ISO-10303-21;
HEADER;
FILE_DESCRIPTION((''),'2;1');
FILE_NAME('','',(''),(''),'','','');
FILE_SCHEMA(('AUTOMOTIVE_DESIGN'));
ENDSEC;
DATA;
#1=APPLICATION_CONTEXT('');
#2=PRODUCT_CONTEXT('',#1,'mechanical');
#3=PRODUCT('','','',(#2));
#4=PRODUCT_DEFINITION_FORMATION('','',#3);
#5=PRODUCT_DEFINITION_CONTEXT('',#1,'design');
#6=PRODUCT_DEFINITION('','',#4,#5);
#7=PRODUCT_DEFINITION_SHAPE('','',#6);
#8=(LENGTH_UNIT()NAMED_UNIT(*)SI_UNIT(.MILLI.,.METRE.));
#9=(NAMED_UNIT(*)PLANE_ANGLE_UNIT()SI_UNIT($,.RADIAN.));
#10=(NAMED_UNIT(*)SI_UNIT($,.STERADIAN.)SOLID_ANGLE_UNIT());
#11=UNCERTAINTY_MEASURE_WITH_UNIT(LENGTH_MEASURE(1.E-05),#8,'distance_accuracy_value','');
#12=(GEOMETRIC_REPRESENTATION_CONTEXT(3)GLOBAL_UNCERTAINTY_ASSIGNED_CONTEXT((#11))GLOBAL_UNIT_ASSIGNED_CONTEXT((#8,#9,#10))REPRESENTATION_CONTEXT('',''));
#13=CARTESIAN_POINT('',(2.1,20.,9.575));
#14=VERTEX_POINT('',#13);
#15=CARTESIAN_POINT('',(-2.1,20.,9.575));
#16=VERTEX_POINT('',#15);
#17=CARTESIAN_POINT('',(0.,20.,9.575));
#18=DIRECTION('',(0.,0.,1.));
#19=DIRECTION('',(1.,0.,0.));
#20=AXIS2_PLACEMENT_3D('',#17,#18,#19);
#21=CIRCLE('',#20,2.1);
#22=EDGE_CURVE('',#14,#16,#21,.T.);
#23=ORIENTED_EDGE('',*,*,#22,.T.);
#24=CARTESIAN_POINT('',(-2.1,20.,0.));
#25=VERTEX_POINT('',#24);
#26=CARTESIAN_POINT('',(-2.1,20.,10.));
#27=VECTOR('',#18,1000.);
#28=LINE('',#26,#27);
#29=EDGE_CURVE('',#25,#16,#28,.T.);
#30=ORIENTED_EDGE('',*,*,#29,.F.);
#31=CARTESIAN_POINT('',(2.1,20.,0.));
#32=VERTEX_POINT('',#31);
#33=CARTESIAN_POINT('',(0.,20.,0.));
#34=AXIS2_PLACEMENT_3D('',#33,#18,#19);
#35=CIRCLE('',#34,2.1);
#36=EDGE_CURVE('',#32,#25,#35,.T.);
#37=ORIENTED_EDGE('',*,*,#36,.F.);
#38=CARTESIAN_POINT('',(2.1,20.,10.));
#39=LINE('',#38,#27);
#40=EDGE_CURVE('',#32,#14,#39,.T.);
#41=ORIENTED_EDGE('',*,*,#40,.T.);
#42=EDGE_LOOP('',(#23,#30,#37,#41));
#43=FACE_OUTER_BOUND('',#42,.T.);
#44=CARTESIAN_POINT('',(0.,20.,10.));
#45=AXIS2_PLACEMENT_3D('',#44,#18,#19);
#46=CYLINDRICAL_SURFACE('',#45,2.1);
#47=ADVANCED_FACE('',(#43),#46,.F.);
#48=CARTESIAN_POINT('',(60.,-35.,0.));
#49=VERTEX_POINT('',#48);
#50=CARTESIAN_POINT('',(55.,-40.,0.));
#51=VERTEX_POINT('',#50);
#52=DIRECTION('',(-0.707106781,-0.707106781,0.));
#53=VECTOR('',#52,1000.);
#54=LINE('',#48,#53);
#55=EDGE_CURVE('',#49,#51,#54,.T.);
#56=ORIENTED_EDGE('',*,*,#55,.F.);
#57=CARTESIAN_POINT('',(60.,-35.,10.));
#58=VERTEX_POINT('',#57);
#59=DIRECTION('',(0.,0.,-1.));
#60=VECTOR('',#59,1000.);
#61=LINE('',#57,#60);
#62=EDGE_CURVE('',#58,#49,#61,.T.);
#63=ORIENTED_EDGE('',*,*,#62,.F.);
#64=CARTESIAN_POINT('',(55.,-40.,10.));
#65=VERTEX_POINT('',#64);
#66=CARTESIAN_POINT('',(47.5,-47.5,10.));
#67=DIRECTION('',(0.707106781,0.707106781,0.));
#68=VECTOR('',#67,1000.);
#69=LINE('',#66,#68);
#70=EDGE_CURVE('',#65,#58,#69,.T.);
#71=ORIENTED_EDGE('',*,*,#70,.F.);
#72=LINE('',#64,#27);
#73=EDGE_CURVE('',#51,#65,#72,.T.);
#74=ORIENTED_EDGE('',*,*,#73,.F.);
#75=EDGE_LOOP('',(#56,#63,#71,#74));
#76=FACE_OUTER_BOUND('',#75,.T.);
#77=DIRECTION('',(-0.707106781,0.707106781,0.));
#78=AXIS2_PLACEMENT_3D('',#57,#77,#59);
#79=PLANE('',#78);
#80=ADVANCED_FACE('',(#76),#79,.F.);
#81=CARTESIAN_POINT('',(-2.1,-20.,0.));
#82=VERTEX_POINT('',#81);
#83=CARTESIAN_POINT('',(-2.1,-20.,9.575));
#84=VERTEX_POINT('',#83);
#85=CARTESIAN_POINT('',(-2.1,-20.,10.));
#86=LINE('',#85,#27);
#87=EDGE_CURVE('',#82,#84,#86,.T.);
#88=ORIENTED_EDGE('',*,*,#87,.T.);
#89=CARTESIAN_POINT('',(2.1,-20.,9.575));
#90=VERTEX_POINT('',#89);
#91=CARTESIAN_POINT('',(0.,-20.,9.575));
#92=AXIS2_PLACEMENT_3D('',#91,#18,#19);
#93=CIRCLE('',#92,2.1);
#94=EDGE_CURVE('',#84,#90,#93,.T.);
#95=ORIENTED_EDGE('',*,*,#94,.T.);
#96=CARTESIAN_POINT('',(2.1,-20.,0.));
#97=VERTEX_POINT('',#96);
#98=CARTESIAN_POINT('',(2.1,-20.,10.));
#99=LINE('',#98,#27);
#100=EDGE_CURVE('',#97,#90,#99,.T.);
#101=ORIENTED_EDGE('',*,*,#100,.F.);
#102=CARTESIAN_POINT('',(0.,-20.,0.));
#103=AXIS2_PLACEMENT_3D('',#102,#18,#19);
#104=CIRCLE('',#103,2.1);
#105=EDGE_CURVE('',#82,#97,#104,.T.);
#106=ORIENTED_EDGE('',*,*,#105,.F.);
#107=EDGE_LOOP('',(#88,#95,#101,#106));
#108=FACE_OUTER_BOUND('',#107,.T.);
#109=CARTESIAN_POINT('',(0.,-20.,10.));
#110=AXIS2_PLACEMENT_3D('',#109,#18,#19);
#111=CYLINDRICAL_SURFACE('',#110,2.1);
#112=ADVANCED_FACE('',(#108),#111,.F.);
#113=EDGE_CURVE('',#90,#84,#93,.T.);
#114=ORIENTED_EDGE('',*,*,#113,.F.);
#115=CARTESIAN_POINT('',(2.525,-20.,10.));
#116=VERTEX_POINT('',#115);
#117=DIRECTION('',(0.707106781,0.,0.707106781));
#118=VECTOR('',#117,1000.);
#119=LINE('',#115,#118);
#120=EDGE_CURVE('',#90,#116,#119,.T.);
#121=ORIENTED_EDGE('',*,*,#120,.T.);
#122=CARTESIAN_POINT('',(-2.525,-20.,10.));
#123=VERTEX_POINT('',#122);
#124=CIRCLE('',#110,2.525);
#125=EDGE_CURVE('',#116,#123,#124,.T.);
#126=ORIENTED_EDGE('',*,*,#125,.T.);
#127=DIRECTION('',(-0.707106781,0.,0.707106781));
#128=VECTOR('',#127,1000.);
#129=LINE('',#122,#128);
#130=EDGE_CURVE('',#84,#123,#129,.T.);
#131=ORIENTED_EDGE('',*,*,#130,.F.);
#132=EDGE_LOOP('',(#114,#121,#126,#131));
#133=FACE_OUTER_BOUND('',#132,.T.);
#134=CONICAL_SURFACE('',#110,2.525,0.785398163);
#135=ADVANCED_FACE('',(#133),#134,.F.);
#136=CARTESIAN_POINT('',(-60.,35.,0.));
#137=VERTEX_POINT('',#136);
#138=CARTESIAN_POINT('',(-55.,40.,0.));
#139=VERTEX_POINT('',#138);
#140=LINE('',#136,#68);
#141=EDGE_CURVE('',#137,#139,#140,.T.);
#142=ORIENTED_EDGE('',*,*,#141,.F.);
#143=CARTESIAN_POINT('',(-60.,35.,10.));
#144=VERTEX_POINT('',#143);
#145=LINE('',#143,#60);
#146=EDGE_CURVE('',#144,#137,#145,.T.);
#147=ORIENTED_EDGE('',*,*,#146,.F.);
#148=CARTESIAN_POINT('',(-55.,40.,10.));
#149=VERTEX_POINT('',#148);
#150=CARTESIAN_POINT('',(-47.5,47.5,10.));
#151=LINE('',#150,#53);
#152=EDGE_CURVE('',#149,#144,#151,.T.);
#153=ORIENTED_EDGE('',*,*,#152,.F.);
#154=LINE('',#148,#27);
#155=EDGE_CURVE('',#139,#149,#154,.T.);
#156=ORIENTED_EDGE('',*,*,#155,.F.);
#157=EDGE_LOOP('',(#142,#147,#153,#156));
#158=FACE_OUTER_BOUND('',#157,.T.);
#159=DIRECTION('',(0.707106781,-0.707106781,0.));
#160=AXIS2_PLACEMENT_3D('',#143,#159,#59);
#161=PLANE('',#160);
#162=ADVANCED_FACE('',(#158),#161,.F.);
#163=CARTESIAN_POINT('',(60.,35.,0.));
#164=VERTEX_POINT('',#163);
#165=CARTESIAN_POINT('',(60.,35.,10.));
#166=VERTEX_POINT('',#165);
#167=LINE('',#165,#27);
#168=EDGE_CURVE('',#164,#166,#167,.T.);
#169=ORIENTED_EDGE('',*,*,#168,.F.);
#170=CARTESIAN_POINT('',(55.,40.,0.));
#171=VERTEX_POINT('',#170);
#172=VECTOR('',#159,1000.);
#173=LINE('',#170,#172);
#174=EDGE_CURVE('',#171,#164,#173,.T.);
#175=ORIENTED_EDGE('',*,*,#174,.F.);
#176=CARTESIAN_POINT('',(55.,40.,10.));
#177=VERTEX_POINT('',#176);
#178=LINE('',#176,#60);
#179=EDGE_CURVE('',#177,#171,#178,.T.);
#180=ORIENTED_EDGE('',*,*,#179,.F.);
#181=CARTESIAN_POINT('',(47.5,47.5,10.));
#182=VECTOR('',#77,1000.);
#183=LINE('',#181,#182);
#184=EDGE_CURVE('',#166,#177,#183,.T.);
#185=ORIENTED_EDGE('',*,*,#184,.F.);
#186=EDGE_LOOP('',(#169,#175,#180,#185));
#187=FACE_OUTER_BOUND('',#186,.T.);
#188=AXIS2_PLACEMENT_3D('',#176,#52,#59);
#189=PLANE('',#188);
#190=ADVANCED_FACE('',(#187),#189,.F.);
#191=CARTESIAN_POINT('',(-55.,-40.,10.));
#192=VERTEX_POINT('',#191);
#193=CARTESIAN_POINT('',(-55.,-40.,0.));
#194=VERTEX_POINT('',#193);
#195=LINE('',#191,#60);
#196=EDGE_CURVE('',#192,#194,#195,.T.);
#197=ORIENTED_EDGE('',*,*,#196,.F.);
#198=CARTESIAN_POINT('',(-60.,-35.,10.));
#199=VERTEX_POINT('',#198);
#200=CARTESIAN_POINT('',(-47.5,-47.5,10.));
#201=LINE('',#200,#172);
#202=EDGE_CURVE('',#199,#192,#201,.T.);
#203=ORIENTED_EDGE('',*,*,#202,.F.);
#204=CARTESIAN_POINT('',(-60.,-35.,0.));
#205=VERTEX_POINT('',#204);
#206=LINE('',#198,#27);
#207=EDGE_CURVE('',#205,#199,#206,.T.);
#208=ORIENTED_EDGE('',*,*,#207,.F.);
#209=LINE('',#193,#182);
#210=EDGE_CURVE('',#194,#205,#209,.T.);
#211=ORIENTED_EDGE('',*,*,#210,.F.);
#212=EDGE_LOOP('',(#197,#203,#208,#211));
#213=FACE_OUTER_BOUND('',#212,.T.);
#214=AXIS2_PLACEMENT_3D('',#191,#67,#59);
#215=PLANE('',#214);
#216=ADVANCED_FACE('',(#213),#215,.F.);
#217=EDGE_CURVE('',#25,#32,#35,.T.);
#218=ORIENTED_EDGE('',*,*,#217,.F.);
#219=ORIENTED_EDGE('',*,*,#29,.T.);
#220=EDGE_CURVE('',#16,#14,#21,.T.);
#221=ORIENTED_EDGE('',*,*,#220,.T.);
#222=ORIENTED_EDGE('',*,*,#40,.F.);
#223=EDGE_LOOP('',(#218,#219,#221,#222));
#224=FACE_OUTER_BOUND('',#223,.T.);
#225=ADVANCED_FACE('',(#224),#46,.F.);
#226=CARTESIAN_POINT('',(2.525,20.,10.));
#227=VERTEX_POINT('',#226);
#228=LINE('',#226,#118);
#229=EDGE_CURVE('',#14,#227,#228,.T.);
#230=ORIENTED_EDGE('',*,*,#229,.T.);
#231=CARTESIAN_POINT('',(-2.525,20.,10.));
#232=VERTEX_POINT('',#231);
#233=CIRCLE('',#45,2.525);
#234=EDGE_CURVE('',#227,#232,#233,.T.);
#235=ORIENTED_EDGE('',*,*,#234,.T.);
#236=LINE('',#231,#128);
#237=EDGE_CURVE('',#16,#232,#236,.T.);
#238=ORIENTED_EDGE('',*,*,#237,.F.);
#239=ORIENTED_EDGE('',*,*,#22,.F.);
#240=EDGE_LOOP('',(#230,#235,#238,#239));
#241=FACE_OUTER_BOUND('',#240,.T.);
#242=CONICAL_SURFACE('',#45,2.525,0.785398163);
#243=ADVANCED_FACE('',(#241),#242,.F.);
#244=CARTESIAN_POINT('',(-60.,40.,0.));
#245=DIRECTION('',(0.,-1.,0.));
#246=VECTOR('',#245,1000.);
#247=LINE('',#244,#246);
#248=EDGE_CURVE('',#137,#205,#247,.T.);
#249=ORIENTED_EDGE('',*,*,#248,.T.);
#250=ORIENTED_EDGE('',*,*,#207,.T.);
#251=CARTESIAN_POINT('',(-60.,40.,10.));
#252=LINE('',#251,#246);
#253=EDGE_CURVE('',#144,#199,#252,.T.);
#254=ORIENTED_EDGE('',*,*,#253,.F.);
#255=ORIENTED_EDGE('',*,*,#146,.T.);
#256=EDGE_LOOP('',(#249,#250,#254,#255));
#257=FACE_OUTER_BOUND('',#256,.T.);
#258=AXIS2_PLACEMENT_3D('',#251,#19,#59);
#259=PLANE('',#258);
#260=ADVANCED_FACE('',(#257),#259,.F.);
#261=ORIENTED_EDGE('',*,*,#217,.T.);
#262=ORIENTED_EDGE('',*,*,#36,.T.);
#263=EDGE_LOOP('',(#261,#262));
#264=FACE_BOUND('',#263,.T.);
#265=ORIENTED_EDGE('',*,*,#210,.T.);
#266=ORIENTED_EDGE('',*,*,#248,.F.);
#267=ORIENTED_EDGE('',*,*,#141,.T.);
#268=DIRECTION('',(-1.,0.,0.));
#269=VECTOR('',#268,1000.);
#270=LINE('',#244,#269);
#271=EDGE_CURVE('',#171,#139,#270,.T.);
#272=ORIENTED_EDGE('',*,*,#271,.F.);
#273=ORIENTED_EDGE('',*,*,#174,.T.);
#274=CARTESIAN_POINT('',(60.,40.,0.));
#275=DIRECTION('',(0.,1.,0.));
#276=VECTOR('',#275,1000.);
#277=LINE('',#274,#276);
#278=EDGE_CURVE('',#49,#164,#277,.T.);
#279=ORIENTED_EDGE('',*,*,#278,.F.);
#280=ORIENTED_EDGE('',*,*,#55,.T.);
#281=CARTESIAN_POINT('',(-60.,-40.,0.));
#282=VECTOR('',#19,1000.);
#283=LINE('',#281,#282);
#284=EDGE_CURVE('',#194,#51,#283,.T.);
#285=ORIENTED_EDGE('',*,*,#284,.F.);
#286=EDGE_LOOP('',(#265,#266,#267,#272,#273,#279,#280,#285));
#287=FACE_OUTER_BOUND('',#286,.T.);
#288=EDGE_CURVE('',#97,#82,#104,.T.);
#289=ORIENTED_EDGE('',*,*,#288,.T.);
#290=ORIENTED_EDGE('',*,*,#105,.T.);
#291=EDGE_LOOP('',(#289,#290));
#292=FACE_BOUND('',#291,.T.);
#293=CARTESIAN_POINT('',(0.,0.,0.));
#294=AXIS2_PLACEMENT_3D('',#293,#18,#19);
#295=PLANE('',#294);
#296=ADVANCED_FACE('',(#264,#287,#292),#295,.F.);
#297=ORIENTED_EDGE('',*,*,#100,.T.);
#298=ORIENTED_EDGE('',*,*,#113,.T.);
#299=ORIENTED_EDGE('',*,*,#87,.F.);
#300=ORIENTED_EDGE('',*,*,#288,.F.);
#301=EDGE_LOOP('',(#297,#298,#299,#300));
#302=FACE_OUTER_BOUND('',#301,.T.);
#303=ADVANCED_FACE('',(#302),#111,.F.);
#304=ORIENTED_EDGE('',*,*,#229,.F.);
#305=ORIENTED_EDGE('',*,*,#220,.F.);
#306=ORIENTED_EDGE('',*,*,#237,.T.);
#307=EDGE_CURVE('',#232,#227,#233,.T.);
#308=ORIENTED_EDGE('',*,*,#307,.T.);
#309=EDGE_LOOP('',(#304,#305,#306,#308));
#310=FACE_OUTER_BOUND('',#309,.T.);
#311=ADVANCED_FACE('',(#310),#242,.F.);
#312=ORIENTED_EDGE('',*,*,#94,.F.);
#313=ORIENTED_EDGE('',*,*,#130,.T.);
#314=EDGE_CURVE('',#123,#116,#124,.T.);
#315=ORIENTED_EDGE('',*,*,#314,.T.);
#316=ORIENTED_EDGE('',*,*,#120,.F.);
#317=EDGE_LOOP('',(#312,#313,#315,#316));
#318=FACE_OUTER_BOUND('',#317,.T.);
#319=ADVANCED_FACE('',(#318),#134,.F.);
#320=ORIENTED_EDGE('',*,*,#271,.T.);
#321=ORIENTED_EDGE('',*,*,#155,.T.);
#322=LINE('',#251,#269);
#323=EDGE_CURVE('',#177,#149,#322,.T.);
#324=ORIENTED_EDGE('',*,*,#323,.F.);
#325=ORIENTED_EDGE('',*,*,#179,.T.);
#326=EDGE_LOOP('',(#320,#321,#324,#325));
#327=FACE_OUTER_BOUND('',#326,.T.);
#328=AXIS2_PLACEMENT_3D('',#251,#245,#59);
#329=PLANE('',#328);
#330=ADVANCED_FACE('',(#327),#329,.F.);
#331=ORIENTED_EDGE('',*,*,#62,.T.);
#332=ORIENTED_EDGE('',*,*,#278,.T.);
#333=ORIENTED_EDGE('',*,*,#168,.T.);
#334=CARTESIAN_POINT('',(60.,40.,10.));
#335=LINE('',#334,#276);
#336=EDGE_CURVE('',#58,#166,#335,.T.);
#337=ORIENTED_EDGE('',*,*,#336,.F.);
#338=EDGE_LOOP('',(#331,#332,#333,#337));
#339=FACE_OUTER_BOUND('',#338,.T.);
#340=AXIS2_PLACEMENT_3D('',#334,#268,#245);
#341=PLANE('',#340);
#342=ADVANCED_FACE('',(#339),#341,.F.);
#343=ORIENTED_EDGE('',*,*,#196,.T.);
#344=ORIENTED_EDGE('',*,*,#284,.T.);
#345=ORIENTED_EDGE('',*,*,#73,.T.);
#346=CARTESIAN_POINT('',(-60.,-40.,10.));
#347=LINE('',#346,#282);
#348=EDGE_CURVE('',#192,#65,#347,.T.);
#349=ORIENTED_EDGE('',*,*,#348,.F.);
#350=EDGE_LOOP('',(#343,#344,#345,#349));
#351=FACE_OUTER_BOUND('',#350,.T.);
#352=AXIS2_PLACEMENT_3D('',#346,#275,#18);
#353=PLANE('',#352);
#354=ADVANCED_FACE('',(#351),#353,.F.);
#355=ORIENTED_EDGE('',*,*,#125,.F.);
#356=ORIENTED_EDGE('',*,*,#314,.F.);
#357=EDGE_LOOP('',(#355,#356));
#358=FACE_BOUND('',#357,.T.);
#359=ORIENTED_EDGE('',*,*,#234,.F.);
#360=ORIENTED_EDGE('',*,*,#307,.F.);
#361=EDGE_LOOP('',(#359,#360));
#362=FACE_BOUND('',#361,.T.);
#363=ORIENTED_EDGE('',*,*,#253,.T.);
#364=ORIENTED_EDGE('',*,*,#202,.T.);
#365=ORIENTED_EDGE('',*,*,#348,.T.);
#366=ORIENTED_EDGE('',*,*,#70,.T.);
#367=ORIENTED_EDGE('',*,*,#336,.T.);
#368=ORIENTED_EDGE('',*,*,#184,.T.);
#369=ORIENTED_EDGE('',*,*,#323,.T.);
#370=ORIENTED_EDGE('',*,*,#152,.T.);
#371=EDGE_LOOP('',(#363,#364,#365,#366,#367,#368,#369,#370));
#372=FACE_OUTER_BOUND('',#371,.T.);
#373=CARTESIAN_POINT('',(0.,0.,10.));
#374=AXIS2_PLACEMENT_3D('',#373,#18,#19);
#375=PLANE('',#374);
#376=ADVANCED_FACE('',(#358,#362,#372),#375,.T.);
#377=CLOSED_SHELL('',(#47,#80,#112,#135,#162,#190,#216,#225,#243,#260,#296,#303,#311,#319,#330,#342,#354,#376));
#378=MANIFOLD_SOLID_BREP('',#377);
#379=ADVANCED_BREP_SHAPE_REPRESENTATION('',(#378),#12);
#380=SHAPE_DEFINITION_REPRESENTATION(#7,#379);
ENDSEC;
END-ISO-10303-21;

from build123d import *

# Parameters (mm, degrees)
SKETCH_1_W                   = 120
SKETCH_1_H                   = 80
EXTRUDE_1_DEPTH              = 10
CHAMFER_1_SIZE               = 5
HOLE_WIZARD_M5_1_D           = 4.2
HOLE_WIZARD_M5_1_DEPTH       = 14
HOLE_WIZARD_M5_1_CSINK_D     = 5.05
HOLE_WIZARD_M5_1_CSINK_ANGLE = 90
HOLE_WIZARD_M5_1_TIP         = 1.2618073


with BuildPart() as part:
    # 草图1 → 凸台-拉伸1 (new body)
    with BuildSketch(Plane.XY):
        Rectangle(SKETCH_1_W, SKETCH_1_H)
    extrude(amount=EXTRUDE_1_DEPTH)

    # 倒角1
    chamfer_1_edges = [part.edges().sort_by_distance(p)[0] for p in [
        (60, -40, 5),
        (-60, -40, 5),
        (-60, 40, 5),
        (60, 40, 5),
    ]]
    chamfer(chamfer_1_edges, length=CHAMFER_1_SIZE)

    # M5 螺纹孔1
    with Locations(Plane(origin=(0, 20, 10), x_dir=(1, 0, 0), z_dir=(0, 0, 1))):
        with Locations((0, 0), (0, -40)):
            CounterSinkHole(HOLE_WIZARD_M5_1_D / 2, HOLE_WIZARD_M5_1_CSINK_D / 2, depth=HOLE_WIZARD_M5_1_DEPTH, counter_sink_angle=HOLE_WIZARD_M5_1_CSINK_ANGLE)
            with Locations((0, 0, -(HOLE_WIZARD_M5_1_DEPTH + HOLE_WIZARD_M5_1_TIP / 2))):  # 118° drill point
                Cone(0, HOLE_WIZARD_M5_1_D / 2, HOLE_WIZARD_M5_1_TIP, mode=Mode.SUBTRACT)


solid = part.part
